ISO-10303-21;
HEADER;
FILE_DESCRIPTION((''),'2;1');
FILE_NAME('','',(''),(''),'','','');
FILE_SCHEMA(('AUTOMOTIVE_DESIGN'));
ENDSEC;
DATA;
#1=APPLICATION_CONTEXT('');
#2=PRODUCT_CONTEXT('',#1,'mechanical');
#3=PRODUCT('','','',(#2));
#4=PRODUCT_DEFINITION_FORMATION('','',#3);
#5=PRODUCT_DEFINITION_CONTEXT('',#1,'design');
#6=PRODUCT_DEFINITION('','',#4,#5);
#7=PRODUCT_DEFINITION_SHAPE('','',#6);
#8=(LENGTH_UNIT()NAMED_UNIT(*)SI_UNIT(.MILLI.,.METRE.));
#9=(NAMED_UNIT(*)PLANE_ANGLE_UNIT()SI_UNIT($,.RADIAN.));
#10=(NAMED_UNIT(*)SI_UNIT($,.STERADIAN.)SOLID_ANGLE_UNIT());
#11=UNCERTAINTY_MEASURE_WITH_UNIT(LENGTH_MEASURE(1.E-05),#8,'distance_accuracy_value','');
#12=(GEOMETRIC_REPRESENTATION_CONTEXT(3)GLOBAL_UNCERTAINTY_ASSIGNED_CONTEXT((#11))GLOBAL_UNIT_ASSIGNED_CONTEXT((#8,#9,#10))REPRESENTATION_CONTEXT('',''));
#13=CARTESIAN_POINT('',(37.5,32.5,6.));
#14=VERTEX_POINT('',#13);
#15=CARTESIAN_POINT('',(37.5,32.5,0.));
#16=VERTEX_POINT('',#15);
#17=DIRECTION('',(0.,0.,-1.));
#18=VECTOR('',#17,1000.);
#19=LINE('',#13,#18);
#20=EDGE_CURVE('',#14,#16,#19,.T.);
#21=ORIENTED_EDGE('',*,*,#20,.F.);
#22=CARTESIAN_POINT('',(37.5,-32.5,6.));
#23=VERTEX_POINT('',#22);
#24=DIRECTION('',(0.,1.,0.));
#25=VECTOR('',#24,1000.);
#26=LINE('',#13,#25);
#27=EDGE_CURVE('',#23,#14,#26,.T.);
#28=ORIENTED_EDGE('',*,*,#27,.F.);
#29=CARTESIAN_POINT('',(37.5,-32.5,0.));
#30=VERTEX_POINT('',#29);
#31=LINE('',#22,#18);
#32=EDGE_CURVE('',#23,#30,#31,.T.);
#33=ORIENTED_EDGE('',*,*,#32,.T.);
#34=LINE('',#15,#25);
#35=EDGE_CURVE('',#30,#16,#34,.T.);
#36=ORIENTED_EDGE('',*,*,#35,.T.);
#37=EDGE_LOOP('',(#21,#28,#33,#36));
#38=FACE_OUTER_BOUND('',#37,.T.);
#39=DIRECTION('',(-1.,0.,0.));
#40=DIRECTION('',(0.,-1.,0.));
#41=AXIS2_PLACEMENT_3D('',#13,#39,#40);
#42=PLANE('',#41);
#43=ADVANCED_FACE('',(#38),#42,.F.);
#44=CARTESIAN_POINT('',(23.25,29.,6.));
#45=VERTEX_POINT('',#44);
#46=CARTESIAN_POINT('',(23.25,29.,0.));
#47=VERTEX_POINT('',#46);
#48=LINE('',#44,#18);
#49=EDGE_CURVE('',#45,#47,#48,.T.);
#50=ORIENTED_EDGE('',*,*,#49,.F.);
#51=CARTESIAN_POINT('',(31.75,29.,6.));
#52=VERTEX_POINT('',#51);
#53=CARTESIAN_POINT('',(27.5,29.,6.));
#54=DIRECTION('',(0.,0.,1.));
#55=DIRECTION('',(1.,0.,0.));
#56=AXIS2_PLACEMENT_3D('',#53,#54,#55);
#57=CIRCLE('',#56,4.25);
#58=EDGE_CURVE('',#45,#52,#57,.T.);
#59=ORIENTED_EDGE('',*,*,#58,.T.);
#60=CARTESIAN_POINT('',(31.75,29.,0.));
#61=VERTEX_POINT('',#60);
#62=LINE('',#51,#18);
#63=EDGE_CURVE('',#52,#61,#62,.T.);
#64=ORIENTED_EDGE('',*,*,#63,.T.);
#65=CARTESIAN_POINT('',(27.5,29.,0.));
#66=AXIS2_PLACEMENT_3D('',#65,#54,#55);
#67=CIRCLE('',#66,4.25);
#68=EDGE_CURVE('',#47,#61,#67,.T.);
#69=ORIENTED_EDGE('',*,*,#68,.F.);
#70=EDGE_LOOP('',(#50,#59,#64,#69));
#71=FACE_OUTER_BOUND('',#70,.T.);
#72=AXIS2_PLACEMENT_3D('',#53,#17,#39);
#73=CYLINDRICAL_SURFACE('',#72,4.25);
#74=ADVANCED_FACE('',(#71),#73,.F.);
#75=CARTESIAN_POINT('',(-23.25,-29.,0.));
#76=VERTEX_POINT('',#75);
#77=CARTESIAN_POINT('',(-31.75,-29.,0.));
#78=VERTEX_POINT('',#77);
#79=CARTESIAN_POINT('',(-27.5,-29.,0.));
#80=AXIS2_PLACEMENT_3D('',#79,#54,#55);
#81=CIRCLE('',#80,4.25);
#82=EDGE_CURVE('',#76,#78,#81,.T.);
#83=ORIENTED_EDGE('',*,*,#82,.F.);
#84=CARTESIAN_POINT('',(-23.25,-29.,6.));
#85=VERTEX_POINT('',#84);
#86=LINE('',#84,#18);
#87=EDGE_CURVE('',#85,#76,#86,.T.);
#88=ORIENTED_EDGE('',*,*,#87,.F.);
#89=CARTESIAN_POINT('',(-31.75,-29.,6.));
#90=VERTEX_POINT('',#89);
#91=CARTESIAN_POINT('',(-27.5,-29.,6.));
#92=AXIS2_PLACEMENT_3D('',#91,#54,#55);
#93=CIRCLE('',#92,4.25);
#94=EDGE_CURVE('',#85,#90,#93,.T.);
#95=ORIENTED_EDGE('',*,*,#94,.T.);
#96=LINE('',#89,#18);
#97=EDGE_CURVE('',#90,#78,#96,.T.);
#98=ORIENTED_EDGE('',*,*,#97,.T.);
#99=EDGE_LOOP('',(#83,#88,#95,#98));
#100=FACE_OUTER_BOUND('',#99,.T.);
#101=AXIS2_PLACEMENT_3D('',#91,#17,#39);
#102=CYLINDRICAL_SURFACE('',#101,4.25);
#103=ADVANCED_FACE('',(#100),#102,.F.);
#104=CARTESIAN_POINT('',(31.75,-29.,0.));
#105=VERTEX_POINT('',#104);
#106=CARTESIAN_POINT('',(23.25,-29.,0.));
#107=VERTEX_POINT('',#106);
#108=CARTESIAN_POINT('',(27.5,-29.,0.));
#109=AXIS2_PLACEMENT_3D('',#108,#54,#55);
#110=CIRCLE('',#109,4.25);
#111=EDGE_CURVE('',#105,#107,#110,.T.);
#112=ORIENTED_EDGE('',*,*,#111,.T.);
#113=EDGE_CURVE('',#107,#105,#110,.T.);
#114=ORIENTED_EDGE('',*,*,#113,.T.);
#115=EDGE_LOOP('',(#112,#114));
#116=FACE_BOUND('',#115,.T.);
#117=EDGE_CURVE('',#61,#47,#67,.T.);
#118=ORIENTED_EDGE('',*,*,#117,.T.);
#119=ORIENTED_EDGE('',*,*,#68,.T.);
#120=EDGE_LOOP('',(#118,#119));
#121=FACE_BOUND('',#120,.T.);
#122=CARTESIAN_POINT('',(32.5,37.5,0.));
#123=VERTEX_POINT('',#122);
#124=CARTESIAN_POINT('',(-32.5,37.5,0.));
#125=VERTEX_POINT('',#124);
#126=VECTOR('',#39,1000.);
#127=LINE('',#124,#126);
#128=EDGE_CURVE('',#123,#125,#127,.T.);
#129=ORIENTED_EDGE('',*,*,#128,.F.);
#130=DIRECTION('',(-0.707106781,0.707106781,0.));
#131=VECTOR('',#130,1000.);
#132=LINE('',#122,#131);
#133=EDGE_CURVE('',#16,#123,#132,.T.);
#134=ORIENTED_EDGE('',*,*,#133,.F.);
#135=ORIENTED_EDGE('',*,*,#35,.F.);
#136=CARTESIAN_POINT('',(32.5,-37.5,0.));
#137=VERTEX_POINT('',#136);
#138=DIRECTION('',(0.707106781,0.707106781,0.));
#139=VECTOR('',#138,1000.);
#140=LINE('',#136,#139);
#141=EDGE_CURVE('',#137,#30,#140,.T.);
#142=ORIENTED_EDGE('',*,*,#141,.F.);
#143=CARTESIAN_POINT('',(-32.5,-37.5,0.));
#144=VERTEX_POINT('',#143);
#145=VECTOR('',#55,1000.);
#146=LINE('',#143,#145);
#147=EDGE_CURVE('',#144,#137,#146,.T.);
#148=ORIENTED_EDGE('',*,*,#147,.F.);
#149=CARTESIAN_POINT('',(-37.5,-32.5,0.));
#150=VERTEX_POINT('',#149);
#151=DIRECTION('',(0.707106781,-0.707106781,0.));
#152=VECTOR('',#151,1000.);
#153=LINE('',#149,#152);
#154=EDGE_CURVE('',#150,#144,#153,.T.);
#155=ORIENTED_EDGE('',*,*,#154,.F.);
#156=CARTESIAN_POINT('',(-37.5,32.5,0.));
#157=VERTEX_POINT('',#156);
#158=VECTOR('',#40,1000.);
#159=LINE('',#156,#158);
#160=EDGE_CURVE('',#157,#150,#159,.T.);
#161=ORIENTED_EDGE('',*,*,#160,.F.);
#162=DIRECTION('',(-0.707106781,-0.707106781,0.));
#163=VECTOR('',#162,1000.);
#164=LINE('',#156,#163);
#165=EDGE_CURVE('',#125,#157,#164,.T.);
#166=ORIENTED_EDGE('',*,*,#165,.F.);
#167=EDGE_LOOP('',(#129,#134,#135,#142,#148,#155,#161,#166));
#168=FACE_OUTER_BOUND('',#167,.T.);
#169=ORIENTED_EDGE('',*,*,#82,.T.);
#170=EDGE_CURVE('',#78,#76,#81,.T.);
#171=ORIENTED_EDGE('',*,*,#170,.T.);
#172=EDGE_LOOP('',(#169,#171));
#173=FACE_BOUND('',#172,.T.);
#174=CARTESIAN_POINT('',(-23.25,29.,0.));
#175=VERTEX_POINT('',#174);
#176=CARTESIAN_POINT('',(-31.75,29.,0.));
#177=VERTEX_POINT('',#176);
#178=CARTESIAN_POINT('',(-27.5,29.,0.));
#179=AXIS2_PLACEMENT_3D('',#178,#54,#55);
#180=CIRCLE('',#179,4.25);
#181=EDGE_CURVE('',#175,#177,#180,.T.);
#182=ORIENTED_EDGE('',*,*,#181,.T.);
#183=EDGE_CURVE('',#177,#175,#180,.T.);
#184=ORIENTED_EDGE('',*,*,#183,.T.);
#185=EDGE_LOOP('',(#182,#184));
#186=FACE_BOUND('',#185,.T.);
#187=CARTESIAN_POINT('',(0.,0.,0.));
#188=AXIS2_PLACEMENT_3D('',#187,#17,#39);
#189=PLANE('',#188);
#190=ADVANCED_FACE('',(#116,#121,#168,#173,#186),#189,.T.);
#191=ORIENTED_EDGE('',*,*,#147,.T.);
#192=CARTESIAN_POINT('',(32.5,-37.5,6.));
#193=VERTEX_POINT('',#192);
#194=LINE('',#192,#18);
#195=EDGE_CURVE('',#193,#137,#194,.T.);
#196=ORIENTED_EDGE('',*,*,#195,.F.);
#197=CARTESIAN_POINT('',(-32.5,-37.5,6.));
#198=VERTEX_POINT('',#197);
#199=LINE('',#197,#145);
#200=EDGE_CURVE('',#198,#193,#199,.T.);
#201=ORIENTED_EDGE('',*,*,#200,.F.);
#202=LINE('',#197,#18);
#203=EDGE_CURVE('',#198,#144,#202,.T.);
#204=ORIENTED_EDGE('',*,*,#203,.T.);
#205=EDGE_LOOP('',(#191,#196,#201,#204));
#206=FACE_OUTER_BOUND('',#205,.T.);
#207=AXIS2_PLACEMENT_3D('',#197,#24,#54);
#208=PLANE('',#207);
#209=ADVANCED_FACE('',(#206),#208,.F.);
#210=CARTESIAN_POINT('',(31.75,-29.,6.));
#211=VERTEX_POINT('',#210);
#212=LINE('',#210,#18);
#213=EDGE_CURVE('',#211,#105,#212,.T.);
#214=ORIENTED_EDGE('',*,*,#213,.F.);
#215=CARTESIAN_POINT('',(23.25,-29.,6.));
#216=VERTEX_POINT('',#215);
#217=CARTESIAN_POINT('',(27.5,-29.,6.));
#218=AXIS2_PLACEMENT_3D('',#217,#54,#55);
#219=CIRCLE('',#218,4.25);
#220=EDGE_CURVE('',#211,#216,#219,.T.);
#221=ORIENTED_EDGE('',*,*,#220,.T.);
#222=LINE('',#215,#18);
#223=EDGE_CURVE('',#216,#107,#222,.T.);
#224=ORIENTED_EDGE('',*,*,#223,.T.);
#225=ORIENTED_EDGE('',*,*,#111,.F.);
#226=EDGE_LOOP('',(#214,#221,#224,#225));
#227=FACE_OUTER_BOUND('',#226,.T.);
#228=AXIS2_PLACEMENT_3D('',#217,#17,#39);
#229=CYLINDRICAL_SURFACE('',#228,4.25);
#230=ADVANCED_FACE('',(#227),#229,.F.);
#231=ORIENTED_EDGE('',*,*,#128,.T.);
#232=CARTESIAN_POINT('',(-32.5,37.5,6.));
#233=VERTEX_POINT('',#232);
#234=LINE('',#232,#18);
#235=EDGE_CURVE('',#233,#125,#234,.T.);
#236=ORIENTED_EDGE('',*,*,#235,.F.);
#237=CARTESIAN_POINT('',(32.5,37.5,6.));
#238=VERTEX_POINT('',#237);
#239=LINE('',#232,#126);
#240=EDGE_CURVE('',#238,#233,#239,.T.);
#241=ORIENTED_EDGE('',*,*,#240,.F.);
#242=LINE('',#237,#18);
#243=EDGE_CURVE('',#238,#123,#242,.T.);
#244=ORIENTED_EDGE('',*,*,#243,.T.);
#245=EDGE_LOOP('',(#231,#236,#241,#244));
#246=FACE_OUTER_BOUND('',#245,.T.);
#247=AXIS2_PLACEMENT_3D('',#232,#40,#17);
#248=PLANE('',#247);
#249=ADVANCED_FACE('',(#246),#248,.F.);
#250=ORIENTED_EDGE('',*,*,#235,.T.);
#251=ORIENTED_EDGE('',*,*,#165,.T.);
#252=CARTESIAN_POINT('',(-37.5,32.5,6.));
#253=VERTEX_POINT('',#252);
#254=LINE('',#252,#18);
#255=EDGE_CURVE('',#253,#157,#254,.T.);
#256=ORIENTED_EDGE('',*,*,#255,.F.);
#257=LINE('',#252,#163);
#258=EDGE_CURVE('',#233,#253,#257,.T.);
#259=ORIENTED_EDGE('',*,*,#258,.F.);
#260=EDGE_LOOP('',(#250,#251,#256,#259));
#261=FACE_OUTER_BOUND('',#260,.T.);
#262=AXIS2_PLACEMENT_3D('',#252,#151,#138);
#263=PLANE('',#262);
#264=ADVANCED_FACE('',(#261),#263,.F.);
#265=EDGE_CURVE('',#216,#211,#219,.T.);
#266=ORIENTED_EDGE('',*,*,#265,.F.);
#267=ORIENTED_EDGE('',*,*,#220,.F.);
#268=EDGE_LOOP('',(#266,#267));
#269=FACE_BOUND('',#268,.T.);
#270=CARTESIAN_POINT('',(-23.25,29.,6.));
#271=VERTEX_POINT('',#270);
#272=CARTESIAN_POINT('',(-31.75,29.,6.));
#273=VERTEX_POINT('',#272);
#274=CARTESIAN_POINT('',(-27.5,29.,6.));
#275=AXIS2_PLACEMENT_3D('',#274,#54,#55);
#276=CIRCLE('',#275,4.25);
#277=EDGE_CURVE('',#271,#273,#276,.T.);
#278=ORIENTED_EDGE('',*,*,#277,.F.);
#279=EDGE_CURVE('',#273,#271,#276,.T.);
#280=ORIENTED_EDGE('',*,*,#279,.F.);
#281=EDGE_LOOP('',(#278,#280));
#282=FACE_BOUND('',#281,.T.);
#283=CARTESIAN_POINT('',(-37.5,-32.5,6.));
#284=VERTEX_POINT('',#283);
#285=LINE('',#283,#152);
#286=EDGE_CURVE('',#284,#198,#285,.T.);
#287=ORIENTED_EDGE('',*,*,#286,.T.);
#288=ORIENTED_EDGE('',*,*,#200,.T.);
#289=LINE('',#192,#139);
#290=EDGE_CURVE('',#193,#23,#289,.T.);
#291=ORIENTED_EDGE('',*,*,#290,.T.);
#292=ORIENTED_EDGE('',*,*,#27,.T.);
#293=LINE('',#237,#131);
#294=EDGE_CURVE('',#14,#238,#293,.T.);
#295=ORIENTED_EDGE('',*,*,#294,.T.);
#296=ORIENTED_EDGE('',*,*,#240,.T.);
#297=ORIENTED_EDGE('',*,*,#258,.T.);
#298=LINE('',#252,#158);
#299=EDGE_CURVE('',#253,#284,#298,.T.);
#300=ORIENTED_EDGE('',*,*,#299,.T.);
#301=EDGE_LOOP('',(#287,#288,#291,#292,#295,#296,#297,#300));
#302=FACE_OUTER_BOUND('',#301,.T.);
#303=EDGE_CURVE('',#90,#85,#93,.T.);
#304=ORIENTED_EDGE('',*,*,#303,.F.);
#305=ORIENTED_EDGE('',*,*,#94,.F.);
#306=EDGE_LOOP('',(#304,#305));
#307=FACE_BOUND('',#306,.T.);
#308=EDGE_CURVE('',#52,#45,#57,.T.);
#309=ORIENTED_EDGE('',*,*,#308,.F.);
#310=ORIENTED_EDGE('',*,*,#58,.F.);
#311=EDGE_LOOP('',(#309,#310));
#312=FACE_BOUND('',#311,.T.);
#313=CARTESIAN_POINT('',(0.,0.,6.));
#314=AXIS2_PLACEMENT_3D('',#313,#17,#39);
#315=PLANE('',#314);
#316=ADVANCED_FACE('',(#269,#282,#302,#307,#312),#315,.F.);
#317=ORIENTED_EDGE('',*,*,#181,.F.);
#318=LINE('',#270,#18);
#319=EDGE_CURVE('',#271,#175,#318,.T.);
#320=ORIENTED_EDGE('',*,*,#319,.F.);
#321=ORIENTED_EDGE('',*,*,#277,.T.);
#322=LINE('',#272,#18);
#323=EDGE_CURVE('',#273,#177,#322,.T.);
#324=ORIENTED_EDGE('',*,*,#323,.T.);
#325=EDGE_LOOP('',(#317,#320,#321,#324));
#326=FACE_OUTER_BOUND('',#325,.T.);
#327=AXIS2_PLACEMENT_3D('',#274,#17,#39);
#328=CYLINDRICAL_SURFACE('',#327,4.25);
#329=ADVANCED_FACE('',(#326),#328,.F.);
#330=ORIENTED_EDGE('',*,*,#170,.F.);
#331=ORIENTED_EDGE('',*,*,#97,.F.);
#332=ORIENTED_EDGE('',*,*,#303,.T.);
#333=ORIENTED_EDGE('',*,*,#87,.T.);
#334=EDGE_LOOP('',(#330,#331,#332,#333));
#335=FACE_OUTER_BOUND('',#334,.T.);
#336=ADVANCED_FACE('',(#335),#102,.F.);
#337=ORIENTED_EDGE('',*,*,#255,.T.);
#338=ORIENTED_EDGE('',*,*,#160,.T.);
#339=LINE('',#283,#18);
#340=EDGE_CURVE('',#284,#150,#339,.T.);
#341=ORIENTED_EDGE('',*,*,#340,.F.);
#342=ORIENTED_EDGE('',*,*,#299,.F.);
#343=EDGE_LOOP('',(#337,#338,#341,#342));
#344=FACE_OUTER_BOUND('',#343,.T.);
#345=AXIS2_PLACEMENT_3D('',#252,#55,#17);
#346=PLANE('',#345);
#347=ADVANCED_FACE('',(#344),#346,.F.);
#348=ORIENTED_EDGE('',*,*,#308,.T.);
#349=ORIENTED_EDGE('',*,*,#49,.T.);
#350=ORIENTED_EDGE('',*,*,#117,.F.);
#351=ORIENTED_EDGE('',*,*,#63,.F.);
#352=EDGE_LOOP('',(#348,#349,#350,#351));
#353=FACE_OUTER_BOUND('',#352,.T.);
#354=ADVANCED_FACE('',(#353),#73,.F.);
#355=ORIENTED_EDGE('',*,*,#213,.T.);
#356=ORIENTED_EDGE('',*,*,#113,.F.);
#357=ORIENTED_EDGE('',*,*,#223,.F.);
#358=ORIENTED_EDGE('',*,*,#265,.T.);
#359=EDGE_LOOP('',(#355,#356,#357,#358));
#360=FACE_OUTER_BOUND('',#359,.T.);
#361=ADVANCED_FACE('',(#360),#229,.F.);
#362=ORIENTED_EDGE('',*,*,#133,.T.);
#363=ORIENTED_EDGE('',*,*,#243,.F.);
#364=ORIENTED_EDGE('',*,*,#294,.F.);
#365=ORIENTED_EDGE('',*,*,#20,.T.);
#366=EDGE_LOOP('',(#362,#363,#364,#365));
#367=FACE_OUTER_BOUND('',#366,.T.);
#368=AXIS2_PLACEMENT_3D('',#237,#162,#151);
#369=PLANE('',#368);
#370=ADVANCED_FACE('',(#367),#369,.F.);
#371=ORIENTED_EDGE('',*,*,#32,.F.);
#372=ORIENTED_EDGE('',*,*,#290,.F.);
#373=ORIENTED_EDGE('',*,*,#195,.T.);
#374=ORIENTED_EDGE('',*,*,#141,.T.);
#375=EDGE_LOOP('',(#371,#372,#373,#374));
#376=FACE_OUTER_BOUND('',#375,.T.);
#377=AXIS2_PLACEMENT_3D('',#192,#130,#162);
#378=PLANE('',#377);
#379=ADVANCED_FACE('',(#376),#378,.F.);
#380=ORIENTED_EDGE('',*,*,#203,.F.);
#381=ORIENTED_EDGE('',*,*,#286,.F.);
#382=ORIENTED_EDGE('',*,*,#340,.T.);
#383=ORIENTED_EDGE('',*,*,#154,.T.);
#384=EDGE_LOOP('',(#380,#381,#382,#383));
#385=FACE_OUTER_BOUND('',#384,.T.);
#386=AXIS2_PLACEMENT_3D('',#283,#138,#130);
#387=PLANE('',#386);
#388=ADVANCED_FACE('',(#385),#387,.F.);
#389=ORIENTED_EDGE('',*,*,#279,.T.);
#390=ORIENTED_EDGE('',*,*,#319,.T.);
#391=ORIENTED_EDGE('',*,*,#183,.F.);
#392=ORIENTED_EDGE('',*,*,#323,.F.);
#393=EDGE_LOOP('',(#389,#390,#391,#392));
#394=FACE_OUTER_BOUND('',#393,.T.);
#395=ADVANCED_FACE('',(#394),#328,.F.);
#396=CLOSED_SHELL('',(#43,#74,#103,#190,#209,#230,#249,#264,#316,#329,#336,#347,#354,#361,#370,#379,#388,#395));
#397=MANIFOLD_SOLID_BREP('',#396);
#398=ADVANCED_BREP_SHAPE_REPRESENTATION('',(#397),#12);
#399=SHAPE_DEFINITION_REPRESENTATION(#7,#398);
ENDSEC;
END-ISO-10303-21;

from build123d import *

# Parameters (mm, degrees)
SKETCH1_R           = 4.25
BOSS_EXTRUDE1_DEPTH = 6


with BuildPart() as part:
    # Sketch1 → Boss-Extrude1 (new body)
    with BuildSketch(Plane.XY):
        Polygon((-37.5, 32.5), (-32.5, 37.5), (32.5, 37.5), (37.5, 32.5), (37.5, -32.5), (32.5, -37.5), (-32.5, -37.5), (-37.5, -32.5), align=None)
        with Locations((-27.5, 29)):
            Circle(SKETCH1_R, mode=Mode.SUBTRACT)
        with Locations((27.5, 29)):
            Circle(SKETCH1_R, mode=Mode.SUBTRACT)
        with Locations((-27.5, -29)):
            Circle(SKETCH1_R, mode=Mode.SUBTRACT)
        with Locations((27.5, -29)):
            Circle(SKETCH1_R, mode=Mode.SUBTRACT)
    extrude(amount=BOSS_EXTRUDE1_DEPTH)


solid = part.part
